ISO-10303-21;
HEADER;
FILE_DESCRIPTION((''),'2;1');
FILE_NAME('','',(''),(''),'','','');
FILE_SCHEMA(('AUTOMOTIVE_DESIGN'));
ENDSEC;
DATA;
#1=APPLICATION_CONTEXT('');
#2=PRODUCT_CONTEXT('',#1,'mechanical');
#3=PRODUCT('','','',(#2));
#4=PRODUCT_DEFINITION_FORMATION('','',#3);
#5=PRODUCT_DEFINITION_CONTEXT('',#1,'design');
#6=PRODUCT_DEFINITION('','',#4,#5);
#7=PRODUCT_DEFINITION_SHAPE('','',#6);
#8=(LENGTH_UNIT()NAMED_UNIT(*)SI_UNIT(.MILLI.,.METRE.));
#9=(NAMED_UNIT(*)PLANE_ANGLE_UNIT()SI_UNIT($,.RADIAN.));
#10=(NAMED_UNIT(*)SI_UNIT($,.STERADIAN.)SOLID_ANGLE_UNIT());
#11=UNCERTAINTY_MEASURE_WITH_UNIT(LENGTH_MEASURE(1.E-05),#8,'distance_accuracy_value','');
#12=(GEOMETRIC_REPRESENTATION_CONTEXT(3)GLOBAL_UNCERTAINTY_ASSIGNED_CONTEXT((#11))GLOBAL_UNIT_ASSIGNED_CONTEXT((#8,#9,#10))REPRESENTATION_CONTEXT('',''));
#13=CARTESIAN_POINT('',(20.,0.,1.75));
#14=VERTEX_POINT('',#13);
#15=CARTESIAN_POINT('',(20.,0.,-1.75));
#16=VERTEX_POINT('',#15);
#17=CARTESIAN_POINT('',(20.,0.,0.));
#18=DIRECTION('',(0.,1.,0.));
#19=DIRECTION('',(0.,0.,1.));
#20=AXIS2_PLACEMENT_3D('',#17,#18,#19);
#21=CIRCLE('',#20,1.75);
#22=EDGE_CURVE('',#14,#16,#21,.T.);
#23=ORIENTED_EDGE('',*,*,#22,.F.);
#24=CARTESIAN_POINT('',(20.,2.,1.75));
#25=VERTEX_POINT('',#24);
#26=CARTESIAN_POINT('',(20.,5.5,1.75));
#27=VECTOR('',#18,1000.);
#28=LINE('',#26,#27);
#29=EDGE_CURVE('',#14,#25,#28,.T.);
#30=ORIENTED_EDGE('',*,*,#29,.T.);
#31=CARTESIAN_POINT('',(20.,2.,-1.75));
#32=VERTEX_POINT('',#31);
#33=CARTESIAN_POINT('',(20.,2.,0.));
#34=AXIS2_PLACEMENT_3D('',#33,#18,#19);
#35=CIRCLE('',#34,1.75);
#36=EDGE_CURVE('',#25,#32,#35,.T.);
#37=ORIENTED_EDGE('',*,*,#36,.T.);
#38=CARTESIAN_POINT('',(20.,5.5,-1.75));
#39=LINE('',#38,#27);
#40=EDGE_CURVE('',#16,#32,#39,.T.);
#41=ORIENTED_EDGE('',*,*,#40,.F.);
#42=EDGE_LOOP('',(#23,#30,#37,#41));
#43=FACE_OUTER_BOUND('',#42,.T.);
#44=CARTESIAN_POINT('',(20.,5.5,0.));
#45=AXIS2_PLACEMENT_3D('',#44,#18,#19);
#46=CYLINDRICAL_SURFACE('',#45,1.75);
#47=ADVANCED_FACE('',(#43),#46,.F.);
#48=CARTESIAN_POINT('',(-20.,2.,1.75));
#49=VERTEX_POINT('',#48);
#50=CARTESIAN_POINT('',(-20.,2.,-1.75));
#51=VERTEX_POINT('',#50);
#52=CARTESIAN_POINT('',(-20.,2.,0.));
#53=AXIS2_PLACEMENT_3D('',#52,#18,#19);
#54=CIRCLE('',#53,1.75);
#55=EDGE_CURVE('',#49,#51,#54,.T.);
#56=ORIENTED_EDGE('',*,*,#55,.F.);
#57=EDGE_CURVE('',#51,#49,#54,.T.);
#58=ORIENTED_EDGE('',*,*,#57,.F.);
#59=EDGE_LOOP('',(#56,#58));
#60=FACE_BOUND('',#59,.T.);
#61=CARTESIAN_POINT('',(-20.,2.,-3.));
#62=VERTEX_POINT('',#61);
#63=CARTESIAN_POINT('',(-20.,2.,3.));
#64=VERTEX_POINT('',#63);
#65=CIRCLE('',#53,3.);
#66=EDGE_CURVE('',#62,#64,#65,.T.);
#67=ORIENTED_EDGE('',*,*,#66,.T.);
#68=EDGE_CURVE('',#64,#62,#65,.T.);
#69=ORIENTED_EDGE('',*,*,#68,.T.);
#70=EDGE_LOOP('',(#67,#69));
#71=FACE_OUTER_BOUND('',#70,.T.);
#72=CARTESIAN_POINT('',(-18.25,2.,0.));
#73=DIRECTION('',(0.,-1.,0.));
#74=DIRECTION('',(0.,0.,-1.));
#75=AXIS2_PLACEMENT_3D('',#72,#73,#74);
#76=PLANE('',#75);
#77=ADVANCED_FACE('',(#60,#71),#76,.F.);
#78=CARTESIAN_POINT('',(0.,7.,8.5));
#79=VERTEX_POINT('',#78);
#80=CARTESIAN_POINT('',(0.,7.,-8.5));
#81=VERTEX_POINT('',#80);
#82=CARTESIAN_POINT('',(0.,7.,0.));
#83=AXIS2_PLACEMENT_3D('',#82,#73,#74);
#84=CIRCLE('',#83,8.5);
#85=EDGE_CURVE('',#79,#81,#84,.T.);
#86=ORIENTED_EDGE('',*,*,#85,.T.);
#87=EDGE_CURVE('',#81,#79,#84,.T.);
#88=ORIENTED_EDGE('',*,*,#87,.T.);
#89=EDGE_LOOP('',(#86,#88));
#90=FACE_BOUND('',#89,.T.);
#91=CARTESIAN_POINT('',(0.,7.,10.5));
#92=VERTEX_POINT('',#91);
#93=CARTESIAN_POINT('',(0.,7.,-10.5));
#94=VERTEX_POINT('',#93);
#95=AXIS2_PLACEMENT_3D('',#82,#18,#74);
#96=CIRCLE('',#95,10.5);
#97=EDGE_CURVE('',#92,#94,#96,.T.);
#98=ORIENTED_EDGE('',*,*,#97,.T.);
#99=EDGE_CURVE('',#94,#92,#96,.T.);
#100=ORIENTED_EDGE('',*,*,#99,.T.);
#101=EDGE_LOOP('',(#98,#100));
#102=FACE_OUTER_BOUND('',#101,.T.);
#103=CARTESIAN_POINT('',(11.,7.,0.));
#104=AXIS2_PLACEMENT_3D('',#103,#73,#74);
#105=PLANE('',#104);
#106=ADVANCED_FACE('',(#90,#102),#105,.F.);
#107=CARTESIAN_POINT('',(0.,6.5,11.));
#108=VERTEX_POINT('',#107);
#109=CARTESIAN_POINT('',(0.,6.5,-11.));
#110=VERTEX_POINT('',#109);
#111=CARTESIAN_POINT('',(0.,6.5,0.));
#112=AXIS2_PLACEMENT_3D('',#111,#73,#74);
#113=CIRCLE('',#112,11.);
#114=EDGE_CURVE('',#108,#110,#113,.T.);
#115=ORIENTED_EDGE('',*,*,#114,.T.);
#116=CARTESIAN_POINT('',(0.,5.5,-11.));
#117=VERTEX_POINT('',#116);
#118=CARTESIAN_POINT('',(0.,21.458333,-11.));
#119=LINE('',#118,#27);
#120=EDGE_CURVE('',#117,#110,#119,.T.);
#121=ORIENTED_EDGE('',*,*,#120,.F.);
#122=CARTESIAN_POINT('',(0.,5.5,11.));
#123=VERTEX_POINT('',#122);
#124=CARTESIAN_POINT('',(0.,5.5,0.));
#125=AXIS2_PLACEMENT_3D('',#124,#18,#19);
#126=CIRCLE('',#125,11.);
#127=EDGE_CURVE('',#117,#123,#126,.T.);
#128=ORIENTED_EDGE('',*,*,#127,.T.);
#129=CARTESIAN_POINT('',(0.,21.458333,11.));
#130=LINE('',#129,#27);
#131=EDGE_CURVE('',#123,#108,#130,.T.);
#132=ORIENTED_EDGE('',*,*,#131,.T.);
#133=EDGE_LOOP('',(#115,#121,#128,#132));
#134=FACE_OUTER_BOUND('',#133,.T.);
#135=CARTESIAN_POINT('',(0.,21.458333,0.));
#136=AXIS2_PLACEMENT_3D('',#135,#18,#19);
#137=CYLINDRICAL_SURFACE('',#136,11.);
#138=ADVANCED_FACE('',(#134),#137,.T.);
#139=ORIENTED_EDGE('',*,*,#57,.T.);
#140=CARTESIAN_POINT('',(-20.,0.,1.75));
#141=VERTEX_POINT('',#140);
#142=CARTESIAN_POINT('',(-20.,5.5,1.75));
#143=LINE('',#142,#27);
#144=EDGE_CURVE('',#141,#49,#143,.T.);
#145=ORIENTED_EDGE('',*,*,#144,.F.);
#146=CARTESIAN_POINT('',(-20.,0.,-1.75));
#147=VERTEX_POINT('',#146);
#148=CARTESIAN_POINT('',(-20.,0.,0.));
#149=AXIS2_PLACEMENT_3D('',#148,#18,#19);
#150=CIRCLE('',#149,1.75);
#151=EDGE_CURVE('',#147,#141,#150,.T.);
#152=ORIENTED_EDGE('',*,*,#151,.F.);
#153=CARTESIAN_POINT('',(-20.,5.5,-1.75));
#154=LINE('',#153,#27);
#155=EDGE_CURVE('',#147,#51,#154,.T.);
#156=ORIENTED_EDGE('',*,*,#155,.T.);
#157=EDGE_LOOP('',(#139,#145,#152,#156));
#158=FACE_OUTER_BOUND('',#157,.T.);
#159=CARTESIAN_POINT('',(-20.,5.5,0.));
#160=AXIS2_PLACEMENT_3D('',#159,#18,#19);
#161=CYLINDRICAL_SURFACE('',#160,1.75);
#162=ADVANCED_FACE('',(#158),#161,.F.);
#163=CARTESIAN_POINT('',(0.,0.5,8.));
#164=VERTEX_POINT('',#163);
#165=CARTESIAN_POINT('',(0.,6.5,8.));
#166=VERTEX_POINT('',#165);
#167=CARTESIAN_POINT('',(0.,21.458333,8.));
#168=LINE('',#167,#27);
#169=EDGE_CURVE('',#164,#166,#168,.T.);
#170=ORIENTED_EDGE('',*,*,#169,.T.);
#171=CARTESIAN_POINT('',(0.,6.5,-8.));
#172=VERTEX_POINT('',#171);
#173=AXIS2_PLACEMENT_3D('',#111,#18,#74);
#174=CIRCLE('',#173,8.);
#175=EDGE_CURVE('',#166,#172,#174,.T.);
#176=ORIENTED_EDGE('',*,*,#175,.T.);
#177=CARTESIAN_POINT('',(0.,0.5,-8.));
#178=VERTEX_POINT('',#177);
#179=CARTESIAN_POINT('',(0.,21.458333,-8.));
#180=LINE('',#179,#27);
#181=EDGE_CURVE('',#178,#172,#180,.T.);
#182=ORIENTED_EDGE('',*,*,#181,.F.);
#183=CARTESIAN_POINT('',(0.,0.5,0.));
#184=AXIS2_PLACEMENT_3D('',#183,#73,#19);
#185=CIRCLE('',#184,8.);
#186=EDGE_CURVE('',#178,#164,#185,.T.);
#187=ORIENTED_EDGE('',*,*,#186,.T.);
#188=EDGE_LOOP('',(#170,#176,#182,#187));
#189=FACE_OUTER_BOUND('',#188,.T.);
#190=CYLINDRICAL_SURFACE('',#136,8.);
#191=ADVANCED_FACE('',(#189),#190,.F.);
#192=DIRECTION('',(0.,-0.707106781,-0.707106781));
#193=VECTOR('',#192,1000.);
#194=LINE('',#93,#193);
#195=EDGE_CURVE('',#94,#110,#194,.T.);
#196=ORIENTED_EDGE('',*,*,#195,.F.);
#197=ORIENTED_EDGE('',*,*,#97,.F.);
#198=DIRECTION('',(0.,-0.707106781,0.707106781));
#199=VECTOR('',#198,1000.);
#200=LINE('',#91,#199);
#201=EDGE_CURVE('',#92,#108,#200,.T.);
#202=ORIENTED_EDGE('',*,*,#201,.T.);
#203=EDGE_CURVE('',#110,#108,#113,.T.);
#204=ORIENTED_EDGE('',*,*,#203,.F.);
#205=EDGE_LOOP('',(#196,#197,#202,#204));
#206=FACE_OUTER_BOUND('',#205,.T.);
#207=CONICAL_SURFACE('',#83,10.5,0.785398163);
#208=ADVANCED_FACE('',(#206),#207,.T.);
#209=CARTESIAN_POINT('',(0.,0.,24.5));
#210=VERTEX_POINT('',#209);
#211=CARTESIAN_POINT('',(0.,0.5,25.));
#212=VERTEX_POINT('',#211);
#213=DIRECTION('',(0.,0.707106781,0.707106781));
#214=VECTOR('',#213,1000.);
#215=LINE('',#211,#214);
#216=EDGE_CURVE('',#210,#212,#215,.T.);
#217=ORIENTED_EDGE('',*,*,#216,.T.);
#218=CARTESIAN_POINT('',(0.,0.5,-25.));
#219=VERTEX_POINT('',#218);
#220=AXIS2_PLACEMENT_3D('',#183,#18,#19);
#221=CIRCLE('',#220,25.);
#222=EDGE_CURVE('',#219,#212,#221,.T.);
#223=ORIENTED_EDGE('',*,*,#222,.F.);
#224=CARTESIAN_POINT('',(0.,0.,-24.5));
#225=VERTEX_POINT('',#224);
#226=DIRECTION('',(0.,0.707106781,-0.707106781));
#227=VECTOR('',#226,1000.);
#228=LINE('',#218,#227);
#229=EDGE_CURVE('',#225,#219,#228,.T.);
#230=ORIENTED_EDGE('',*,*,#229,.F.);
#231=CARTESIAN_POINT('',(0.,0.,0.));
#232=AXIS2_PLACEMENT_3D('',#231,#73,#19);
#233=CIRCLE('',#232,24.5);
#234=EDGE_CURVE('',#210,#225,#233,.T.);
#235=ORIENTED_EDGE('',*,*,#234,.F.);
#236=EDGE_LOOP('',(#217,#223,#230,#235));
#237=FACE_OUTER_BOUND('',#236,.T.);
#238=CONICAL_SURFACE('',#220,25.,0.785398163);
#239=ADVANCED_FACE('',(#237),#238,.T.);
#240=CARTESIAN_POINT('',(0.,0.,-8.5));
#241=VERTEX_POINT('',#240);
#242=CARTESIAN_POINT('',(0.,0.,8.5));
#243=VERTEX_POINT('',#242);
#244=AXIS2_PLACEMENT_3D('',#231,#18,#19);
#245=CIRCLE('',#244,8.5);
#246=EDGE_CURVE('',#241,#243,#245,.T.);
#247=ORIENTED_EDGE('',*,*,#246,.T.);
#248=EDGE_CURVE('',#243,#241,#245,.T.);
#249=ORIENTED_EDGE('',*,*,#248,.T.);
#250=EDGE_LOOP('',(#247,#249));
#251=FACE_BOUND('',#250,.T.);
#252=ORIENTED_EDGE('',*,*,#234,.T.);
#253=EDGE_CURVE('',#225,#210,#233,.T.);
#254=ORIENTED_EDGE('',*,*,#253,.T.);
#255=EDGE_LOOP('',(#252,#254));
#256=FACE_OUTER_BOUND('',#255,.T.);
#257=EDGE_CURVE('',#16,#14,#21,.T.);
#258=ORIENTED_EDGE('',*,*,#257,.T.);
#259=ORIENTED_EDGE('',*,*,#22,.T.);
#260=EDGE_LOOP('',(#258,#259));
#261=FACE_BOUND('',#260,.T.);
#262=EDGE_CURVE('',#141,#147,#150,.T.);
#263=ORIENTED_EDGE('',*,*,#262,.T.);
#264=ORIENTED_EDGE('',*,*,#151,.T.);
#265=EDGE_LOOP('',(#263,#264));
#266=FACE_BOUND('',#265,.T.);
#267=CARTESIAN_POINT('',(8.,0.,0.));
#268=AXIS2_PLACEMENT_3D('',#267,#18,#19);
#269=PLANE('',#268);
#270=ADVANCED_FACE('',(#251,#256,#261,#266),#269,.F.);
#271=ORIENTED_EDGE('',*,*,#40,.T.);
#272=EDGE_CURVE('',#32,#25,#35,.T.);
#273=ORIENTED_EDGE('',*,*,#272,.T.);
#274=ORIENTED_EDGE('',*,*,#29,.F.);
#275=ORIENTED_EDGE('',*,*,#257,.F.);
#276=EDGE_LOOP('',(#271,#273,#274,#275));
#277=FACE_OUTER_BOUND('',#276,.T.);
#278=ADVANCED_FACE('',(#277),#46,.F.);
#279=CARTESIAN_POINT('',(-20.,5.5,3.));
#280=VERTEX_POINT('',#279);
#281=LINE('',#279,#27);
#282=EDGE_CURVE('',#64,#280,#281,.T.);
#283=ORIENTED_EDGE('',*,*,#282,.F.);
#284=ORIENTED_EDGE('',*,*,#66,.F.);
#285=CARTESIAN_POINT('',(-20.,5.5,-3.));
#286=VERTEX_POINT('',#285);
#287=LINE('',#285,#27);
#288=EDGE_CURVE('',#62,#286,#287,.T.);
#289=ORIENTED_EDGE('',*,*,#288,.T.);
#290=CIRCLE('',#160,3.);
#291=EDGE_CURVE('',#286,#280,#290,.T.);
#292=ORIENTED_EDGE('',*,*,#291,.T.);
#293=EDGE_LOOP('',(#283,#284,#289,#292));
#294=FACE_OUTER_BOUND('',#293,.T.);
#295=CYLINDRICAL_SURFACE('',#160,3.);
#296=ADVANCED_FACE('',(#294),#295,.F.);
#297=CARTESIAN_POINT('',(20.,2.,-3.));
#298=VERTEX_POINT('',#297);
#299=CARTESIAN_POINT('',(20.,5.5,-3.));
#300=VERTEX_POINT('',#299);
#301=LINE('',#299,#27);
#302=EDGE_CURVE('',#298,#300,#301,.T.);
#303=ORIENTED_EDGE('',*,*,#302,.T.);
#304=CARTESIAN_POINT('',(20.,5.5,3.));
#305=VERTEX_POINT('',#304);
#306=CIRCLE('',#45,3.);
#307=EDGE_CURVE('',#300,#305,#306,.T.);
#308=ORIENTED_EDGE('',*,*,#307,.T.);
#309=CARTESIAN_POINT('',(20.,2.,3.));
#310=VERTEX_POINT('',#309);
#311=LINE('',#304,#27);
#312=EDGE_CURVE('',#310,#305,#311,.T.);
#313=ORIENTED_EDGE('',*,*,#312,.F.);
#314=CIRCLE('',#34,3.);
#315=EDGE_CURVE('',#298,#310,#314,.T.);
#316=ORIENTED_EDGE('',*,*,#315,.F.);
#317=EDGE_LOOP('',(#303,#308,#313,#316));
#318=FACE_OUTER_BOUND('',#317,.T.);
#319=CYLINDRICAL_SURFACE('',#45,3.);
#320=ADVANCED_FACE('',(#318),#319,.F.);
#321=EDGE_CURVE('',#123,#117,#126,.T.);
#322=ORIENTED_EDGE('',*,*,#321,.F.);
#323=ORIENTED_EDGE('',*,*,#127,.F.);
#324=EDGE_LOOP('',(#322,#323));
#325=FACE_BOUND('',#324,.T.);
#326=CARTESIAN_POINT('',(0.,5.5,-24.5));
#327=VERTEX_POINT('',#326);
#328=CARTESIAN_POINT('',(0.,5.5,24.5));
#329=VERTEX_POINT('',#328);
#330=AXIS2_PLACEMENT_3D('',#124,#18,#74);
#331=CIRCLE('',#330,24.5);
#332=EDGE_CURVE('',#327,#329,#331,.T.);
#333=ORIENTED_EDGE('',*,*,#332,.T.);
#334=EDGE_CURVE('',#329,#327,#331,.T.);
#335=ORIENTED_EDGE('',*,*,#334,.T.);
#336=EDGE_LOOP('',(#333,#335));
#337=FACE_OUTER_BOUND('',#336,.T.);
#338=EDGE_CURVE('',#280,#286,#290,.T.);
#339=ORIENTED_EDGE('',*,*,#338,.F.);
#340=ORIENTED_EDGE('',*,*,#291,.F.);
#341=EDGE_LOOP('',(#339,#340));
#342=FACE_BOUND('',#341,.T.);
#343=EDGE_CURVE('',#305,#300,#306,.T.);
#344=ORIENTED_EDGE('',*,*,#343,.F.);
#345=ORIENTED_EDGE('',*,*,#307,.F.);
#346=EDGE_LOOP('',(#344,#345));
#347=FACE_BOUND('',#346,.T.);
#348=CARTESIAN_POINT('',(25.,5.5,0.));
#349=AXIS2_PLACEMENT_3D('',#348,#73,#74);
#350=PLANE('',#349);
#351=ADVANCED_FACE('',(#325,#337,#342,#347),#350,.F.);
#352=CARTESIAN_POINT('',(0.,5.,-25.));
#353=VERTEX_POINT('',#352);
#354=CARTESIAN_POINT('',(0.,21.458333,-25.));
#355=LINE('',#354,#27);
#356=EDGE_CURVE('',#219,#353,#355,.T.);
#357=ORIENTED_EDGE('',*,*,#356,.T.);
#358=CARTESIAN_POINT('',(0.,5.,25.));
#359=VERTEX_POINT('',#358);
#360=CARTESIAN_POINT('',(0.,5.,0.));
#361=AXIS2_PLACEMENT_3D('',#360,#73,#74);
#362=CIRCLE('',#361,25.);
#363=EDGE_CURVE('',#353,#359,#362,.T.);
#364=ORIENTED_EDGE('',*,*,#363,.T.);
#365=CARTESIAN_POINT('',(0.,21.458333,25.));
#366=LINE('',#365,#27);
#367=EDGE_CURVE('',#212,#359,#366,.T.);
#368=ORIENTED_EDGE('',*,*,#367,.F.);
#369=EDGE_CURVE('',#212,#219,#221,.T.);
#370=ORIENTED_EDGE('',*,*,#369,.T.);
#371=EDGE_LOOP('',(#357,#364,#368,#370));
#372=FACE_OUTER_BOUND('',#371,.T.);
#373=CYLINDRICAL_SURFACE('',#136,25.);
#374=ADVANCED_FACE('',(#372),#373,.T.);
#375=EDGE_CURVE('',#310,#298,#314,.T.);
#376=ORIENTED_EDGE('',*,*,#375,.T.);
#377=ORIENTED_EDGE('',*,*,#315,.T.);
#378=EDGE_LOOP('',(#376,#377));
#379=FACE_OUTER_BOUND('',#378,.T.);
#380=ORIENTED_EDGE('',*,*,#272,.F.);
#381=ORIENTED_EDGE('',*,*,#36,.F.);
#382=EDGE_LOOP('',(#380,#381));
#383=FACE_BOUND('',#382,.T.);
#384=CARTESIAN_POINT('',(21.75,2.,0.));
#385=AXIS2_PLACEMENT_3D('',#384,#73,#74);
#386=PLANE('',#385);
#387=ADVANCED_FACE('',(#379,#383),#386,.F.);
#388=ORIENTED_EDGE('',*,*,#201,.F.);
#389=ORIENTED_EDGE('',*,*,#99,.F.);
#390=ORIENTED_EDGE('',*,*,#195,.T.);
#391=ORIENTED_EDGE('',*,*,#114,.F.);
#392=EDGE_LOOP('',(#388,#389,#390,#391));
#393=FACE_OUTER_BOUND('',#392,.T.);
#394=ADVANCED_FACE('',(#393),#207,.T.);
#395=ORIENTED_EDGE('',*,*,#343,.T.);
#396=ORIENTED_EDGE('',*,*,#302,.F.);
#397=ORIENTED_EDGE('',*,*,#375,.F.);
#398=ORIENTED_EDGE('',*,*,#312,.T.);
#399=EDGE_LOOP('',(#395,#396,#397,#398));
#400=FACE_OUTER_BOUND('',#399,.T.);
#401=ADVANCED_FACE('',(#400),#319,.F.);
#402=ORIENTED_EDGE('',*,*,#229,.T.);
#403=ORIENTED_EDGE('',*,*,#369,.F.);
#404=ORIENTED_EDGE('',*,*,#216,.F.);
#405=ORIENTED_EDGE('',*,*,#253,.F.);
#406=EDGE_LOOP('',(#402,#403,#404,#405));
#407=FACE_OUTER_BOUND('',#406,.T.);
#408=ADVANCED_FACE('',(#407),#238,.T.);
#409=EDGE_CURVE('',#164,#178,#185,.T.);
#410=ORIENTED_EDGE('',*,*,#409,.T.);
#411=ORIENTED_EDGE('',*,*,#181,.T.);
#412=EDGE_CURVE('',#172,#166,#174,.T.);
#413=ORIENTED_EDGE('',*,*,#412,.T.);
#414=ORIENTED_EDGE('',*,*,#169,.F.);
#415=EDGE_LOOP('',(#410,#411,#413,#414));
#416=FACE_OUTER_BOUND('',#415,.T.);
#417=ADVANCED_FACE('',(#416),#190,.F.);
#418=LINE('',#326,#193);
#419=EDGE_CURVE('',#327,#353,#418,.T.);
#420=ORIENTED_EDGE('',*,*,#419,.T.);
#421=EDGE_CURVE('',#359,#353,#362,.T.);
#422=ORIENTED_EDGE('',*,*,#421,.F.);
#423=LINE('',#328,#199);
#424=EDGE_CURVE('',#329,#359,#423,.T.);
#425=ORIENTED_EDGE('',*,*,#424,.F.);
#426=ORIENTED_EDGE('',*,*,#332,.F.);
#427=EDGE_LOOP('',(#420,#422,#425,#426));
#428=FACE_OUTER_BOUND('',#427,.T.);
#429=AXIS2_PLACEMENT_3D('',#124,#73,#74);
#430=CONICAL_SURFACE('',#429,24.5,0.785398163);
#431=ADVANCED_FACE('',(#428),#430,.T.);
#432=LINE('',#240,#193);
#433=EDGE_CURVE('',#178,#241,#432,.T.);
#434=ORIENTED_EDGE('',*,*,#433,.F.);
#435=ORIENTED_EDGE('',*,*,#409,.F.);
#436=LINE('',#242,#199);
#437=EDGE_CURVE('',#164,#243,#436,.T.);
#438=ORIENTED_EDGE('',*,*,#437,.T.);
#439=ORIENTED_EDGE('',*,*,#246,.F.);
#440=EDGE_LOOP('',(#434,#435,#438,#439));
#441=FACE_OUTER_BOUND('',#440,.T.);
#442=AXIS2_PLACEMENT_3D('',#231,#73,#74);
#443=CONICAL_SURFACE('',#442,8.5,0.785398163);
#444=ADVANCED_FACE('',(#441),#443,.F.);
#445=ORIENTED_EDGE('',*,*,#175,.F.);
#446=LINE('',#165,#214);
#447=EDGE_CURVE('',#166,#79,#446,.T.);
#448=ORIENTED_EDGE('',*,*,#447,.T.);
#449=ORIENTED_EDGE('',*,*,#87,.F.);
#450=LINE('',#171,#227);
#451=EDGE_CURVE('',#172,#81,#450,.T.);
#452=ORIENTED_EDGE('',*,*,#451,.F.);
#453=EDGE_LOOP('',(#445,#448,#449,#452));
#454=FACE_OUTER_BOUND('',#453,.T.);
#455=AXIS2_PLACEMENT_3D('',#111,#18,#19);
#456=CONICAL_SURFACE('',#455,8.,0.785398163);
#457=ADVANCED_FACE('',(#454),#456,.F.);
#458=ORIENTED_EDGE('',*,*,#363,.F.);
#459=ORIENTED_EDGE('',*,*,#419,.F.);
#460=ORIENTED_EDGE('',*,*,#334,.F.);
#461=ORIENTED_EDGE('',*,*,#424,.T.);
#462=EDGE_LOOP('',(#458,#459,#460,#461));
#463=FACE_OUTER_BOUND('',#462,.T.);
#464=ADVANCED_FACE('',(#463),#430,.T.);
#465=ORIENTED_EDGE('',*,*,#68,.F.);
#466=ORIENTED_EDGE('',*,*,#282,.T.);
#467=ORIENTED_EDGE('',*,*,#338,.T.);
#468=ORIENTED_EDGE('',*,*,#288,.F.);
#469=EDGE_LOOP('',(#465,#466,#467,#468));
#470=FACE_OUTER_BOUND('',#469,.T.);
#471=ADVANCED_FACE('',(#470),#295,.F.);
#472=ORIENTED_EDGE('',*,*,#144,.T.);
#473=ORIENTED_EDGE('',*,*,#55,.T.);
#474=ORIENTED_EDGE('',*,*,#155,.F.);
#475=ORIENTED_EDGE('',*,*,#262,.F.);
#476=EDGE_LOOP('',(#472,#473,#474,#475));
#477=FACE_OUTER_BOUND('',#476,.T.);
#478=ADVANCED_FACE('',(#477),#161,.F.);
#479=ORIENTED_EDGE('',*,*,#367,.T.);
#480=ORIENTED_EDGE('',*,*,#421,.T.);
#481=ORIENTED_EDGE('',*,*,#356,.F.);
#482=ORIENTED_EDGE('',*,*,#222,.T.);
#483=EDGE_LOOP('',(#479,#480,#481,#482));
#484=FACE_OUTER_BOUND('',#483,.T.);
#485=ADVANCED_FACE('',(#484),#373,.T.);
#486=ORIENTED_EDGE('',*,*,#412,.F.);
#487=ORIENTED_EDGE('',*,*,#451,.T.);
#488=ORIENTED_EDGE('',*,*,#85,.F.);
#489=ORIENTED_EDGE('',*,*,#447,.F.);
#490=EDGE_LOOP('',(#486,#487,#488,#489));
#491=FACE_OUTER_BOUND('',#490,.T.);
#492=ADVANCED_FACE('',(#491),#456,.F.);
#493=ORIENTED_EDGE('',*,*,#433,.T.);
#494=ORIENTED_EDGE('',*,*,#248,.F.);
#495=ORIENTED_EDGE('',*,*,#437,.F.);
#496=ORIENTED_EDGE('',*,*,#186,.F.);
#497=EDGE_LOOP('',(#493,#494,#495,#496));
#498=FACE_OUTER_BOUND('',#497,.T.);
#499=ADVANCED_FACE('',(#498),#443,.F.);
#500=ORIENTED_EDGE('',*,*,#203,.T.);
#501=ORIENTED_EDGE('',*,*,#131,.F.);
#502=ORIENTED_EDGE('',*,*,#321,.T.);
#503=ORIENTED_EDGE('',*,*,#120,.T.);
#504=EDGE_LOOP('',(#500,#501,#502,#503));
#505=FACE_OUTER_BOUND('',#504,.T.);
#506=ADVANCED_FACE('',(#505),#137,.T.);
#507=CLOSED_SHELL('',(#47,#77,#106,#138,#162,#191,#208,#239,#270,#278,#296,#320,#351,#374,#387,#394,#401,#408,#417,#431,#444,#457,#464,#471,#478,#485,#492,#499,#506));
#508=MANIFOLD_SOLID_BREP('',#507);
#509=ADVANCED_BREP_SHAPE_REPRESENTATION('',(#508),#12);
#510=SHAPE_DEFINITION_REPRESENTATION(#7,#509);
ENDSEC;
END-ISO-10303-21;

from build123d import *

# Parameters (mm, degrees)
CBORE_FOR_M3_HEX_HEAD_BOLT1_D           = 3.5
CBORE_FOR_M3_HEX_HEAD_BOLT1_CBORE_D     = 6
CBORE_FOR_M3_HEX_HEAD_BOLT1_CBORE_DEPTH = 3.5
CHAMFER1_SIZE                           = 0.5


with BuildPart() as part:
    # Sketch1 → Revolve1 (revolve)
    with BuildSketch(Plane.XY, mode=Mode.PRIVATE) as revolve1_sk:
        Polygon((8, 0), (25, 0), (25, 5.5), (11, 5.5), (11, 7), (8, 7), align=None)
    revolve(revolve1_sk.sketch.rotate(Axis((0, 21.458333333, 0), (0, -1, 0)), 90), axis=Axis((0, 21.458333333, 0), (0, -1, 0)))

    # CBORE for M3 Hex Head Bolt1 (through all)
    with Locations(Plane(origin=(-20, 5.5, 0), x_dir=(0, 0, 1), z_dir=(0, 1, 0))):
        with Locations((0, 0), (0, 40)):
            CounterBoreHole(CBORE_FOR_M3_HEX_HEAD_BOLT1_D / 2, CBORE_FOR_M3_HEX_HEAD_BOLT1_CBORE_D / 2, CBORE_FOR_M3_HEX_HEAD_BOLT1_CBORE_DEPTH)

    # Chamfer1
    chamfer1_edges = [part.edges().sort_by_distance(p)[0] for p in [
        (0, 0, -25),
        (0, 0, -8),
        (0, 7, -8),
        (0, 7, -11),
        (0, 5.5, -25),
    ]]
    chamfer(chamfer1_edges, length=CHAMFER1_SIZE)


solid = part.part
